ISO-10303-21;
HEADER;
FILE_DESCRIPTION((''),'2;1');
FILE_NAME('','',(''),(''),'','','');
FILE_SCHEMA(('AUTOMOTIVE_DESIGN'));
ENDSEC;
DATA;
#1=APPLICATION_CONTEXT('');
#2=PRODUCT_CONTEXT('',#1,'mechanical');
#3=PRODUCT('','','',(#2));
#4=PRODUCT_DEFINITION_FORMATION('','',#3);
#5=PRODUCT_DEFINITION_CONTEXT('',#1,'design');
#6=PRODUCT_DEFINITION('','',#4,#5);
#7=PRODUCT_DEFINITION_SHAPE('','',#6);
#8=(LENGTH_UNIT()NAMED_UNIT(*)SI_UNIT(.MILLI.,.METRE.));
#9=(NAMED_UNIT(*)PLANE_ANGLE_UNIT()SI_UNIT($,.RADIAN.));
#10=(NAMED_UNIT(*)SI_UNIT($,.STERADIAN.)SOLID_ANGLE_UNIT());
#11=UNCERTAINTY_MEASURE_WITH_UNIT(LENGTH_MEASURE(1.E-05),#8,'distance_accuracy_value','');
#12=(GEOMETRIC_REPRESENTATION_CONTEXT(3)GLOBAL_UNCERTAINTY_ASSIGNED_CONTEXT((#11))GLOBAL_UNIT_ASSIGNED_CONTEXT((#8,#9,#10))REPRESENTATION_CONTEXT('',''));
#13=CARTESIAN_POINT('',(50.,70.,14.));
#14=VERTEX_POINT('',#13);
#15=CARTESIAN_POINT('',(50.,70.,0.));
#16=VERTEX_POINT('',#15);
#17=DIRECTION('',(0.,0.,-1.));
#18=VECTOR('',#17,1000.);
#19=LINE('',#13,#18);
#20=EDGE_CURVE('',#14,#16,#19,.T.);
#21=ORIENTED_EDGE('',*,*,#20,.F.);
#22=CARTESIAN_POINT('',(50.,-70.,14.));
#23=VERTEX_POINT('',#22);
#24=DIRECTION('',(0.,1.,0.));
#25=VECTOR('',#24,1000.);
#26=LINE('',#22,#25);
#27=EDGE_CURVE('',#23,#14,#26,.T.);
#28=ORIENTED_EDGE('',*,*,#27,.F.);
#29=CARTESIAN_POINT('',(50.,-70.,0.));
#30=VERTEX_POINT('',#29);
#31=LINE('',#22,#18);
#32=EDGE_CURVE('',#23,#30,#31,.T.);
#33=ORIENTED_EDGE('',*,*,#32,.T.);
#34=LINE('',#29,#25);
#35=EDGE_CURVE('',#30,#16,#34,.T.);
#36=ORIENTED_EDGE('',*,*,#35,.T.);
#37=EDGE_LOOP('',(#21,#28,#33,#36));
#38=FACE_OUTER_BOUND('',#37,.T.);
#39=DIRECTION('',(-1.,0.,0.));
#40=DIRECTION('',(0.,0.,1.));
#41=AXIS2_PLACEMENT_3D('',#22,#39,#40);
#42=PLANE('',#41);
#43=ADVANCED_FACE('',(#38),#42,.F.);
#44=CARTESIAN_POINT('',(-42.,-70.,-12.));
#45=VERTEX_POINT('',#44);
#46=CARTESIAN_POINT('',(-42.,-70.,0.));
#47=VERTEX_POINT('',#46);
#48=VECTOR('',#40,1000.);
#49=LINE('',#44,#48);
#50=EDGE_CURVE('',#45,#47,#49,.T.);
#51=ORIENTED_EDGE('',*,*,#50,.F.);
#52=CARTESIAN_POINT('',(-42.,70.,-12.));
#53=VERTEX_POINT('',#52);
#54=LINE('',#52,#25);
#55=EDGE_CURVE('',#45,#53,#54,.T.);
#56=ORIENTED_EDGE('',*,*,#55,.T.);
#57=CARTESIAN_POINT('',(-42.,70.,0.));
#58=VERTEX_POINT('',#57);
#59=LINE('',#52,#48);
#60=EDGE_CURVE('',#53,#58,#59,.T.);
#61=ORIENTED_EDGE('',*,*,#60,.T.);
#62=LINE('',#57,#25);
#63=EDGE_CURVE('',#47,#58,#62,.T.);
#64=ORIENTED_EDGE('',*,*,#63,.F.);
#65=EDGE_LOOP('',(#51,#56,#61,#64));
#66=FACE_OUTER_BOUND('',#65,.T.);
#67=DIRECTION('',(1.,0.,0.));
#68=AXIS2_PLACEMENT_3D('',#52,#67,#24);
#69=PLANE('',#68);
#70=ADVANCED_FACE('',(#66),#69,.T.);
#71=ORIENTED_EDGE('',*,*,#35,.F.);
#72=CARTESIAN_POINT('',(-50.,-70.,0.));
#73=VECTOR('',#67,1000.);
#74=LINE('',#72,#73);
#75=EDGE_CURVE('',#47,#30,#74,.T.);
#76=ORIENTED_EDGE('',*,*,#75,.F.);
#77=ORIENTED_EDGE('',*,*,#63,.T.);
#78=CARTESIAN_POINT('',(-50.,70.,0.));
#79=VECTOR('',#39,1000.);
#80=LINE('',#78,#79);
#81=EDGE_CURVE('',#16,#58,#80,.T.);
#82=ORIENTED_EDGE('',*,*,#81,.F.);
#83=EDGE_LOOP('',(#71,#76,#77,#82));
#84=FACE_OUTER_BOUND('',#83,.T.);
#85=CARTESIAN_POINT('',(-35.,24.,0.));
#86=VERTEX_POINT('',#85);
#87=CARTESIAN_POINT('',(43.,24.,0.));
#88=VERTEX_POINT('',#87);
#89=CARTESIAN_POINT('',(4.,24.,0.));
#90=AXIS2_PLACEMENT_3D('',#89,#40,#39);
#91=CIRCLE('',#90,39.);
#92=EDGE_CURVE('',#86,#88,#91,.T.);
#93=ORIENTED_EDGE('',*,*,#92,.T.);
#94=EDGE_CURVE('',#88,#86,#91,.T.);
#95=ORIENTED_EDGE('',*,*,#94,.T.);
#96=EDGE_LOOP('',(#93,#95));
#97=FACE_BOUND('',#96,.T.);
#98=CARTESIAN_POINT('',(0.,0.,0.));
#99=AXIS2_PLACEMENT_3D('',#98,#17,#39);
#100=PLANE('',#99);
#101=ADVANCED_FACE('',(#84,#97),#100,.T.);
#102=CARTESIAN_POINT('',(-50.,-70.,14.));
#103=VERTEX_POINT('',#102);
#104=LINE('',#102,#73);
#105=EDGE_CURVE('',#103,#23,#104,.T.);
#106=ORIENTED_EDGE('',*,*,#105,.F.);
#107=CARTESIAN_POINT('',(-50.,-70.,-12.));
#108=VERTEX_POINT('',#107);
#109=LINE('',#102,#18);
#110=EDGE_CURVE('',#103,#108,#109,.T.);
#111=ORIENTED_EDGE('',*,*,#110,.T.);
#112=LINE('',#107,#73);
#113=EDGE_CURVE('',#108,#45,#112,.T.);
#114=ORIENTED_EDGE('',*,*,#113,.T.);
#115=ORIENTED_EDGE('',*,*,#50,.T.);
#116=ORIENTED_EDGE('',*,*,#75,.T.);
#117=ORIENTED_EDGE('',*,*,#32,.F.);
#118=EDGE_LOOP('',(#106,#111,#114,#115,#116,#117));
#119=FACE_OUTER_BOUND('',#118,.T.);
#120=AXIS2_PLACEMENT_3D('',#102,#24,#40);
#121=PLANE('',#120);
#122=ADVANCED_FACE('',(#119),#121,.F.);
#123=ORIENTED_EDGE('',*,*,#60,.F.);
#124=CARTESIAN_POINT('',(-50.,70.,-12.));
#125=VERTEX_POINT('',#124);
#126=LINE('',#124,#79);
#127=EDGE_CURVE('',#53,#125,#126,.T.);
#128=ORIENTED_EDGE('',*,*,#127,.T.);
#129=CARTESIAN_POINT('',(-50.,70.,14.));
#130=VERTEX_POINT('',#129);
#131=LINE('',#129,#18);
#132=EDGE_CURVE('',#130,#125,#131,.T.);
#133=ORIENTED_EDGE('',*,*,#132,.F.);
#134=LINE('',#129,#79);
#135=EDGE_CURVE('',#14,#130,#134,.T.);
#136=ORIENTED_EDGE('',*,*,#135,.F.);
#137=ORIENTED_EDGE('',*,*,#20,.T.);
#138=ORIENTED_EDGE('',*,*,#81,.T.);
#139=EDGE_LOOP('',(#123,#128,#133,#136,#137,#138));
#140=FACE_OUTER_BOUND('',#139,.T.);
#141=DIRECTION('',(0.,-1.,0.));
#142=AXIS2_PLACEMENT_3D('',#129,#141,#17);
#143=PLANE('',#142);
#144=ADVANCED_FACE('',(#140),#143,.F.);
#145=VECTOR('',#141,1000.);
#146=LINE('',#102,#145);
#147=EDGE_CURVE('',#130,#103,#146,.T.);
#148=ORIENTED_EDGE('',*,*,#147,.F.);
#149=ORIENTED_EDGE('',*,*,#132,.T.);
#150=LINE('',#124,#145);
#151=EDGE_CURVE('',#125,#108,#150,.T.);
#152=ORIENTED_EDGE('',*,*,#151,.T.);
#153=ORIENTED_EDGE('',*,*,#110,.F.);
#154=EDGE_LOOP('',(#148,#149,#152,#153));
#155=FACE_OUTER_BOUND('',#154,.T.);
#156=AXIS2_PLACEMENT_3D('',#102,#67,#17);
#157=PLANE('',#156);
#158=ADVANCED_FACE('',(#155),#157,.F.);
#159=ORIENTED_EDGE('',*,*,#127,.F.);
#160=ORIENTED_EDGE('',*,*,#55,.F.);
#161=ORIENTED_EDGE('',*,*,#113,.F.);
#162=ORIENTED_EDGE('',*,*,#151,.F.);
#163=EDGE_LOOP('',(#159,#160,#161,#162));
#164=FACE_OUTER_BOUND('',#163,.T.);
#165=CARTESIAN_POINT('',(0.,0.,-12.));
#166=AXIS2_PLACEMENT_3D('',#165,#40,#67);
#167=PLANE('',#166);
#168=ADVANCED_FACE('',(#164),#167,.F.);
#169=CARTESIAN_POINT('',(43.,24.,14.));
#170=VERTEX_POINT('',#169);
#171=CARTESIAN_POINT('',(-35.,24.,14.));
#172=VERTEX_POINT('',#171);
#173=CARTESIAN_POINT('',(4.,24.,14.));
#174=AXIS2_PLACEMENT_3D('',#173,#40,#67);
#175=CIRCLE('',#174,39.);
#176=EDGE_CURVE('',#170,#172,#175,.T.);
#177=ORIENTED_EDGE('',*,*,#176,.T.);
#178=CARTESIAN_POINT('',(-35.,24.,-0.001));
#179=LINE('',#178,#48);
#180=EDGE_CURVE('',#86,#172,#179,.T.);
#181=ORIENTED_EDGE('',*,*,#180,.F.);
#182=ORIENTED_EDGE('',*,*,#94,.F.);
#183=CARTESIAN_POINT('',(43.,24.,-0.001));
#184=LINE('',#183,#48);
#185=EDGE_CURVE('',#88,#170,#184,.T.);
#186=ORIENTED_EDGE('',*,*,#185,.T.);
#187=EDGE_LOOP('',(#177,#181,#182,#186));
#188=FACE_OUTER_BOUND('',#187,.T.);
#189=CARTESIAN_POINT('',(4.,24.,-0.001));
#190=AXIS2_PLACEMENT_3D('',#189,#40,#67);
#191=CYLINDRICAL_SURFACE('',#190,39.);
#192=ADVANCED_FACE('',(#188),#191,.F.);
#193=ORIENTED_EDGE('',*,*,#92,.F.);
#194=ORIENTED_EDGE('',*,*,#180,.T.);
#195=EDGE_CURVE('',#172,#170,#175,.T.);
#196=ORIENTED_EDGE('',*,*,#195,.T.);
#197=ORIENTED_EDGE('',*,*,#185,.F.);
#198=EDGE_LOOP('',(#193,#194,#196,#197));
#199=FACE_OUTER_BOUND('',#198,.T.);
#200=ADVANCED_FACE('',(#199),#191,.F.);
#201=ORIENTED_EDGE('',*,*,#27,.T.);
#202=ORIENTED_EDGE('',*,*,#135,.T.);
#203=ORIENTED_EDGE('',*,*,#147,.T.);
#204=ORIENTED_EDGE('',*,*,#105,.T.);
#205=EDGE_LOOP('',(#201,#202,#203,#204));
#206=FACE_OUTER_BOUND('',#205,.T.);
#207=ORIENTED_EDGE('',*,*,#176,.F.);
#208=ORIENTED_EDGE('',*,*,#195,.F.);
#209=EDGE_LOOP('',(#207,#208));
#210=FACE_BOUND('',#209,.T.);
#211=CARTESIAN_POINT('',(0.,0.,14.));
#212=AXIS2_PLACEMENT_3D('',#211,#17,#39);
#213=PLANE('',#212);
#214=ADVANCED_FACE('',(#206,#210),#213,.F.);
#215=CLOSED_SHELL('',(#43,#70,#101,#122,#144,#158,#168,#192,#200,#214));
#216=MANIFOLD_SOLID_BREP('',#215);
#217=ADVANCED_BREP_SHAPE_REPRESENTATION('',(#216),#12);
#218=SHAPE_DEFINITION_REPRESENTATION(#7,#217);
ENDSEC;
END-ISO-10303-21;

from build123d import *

# Parameters (mm, degrees)
SKETCH_1_W          = 100
SKETCH_1_H          = 140
EXTRUDE_1_DEPTH     = 14
CUT_EXTRUDE_1_REACH = 89.155
SKETCH_2_R          = 39
SKETCH_3_W          = 8
SKETCH_3_H          = 140
EXTRUDE_2_DEPTH     = 12


with BuildPart() as part:
    # 草图1 → 凸台-拉伸1 (new body)
    with BuildSketch(Plane.XY):
        Rectangle(SKETCH_1_W, SKETCH_1_H)
    extrude(amount=EXTRUDE_1_DEPTH)

    # 草图2 → 切除-拉伸1 (cut, up to next)
    with BuildSketch(Plane.XY.offset(14), mode=Mode.PRIVATE) as cut_extrude_1_sk1:
        with Locations((4, 24)):
            Circle(SKETCH_2_R)
    cut_extrude_1_tool1 = extrude(cut_extrude_1_sk1.sketch, amount=-CUT_EXTRUDE_1_REACH, mode=Mode.PRIVATE) & part.part
    add(cut_extrude_1_tool1.solids().sort_by_distance((4, 24, 14))[0], mode=Mode.SUBTRACT)

    # 草图3 → 凸台-拉伸2 (add)
    with BuildSketch(Plane.XY):
        with Locations((-46, 0)):
            Rectangle(SKETCH_3_W, SKETCH_3_H)
    extrude(amount=-EXTRUDE_2_DEPTH)


solid = part.part
